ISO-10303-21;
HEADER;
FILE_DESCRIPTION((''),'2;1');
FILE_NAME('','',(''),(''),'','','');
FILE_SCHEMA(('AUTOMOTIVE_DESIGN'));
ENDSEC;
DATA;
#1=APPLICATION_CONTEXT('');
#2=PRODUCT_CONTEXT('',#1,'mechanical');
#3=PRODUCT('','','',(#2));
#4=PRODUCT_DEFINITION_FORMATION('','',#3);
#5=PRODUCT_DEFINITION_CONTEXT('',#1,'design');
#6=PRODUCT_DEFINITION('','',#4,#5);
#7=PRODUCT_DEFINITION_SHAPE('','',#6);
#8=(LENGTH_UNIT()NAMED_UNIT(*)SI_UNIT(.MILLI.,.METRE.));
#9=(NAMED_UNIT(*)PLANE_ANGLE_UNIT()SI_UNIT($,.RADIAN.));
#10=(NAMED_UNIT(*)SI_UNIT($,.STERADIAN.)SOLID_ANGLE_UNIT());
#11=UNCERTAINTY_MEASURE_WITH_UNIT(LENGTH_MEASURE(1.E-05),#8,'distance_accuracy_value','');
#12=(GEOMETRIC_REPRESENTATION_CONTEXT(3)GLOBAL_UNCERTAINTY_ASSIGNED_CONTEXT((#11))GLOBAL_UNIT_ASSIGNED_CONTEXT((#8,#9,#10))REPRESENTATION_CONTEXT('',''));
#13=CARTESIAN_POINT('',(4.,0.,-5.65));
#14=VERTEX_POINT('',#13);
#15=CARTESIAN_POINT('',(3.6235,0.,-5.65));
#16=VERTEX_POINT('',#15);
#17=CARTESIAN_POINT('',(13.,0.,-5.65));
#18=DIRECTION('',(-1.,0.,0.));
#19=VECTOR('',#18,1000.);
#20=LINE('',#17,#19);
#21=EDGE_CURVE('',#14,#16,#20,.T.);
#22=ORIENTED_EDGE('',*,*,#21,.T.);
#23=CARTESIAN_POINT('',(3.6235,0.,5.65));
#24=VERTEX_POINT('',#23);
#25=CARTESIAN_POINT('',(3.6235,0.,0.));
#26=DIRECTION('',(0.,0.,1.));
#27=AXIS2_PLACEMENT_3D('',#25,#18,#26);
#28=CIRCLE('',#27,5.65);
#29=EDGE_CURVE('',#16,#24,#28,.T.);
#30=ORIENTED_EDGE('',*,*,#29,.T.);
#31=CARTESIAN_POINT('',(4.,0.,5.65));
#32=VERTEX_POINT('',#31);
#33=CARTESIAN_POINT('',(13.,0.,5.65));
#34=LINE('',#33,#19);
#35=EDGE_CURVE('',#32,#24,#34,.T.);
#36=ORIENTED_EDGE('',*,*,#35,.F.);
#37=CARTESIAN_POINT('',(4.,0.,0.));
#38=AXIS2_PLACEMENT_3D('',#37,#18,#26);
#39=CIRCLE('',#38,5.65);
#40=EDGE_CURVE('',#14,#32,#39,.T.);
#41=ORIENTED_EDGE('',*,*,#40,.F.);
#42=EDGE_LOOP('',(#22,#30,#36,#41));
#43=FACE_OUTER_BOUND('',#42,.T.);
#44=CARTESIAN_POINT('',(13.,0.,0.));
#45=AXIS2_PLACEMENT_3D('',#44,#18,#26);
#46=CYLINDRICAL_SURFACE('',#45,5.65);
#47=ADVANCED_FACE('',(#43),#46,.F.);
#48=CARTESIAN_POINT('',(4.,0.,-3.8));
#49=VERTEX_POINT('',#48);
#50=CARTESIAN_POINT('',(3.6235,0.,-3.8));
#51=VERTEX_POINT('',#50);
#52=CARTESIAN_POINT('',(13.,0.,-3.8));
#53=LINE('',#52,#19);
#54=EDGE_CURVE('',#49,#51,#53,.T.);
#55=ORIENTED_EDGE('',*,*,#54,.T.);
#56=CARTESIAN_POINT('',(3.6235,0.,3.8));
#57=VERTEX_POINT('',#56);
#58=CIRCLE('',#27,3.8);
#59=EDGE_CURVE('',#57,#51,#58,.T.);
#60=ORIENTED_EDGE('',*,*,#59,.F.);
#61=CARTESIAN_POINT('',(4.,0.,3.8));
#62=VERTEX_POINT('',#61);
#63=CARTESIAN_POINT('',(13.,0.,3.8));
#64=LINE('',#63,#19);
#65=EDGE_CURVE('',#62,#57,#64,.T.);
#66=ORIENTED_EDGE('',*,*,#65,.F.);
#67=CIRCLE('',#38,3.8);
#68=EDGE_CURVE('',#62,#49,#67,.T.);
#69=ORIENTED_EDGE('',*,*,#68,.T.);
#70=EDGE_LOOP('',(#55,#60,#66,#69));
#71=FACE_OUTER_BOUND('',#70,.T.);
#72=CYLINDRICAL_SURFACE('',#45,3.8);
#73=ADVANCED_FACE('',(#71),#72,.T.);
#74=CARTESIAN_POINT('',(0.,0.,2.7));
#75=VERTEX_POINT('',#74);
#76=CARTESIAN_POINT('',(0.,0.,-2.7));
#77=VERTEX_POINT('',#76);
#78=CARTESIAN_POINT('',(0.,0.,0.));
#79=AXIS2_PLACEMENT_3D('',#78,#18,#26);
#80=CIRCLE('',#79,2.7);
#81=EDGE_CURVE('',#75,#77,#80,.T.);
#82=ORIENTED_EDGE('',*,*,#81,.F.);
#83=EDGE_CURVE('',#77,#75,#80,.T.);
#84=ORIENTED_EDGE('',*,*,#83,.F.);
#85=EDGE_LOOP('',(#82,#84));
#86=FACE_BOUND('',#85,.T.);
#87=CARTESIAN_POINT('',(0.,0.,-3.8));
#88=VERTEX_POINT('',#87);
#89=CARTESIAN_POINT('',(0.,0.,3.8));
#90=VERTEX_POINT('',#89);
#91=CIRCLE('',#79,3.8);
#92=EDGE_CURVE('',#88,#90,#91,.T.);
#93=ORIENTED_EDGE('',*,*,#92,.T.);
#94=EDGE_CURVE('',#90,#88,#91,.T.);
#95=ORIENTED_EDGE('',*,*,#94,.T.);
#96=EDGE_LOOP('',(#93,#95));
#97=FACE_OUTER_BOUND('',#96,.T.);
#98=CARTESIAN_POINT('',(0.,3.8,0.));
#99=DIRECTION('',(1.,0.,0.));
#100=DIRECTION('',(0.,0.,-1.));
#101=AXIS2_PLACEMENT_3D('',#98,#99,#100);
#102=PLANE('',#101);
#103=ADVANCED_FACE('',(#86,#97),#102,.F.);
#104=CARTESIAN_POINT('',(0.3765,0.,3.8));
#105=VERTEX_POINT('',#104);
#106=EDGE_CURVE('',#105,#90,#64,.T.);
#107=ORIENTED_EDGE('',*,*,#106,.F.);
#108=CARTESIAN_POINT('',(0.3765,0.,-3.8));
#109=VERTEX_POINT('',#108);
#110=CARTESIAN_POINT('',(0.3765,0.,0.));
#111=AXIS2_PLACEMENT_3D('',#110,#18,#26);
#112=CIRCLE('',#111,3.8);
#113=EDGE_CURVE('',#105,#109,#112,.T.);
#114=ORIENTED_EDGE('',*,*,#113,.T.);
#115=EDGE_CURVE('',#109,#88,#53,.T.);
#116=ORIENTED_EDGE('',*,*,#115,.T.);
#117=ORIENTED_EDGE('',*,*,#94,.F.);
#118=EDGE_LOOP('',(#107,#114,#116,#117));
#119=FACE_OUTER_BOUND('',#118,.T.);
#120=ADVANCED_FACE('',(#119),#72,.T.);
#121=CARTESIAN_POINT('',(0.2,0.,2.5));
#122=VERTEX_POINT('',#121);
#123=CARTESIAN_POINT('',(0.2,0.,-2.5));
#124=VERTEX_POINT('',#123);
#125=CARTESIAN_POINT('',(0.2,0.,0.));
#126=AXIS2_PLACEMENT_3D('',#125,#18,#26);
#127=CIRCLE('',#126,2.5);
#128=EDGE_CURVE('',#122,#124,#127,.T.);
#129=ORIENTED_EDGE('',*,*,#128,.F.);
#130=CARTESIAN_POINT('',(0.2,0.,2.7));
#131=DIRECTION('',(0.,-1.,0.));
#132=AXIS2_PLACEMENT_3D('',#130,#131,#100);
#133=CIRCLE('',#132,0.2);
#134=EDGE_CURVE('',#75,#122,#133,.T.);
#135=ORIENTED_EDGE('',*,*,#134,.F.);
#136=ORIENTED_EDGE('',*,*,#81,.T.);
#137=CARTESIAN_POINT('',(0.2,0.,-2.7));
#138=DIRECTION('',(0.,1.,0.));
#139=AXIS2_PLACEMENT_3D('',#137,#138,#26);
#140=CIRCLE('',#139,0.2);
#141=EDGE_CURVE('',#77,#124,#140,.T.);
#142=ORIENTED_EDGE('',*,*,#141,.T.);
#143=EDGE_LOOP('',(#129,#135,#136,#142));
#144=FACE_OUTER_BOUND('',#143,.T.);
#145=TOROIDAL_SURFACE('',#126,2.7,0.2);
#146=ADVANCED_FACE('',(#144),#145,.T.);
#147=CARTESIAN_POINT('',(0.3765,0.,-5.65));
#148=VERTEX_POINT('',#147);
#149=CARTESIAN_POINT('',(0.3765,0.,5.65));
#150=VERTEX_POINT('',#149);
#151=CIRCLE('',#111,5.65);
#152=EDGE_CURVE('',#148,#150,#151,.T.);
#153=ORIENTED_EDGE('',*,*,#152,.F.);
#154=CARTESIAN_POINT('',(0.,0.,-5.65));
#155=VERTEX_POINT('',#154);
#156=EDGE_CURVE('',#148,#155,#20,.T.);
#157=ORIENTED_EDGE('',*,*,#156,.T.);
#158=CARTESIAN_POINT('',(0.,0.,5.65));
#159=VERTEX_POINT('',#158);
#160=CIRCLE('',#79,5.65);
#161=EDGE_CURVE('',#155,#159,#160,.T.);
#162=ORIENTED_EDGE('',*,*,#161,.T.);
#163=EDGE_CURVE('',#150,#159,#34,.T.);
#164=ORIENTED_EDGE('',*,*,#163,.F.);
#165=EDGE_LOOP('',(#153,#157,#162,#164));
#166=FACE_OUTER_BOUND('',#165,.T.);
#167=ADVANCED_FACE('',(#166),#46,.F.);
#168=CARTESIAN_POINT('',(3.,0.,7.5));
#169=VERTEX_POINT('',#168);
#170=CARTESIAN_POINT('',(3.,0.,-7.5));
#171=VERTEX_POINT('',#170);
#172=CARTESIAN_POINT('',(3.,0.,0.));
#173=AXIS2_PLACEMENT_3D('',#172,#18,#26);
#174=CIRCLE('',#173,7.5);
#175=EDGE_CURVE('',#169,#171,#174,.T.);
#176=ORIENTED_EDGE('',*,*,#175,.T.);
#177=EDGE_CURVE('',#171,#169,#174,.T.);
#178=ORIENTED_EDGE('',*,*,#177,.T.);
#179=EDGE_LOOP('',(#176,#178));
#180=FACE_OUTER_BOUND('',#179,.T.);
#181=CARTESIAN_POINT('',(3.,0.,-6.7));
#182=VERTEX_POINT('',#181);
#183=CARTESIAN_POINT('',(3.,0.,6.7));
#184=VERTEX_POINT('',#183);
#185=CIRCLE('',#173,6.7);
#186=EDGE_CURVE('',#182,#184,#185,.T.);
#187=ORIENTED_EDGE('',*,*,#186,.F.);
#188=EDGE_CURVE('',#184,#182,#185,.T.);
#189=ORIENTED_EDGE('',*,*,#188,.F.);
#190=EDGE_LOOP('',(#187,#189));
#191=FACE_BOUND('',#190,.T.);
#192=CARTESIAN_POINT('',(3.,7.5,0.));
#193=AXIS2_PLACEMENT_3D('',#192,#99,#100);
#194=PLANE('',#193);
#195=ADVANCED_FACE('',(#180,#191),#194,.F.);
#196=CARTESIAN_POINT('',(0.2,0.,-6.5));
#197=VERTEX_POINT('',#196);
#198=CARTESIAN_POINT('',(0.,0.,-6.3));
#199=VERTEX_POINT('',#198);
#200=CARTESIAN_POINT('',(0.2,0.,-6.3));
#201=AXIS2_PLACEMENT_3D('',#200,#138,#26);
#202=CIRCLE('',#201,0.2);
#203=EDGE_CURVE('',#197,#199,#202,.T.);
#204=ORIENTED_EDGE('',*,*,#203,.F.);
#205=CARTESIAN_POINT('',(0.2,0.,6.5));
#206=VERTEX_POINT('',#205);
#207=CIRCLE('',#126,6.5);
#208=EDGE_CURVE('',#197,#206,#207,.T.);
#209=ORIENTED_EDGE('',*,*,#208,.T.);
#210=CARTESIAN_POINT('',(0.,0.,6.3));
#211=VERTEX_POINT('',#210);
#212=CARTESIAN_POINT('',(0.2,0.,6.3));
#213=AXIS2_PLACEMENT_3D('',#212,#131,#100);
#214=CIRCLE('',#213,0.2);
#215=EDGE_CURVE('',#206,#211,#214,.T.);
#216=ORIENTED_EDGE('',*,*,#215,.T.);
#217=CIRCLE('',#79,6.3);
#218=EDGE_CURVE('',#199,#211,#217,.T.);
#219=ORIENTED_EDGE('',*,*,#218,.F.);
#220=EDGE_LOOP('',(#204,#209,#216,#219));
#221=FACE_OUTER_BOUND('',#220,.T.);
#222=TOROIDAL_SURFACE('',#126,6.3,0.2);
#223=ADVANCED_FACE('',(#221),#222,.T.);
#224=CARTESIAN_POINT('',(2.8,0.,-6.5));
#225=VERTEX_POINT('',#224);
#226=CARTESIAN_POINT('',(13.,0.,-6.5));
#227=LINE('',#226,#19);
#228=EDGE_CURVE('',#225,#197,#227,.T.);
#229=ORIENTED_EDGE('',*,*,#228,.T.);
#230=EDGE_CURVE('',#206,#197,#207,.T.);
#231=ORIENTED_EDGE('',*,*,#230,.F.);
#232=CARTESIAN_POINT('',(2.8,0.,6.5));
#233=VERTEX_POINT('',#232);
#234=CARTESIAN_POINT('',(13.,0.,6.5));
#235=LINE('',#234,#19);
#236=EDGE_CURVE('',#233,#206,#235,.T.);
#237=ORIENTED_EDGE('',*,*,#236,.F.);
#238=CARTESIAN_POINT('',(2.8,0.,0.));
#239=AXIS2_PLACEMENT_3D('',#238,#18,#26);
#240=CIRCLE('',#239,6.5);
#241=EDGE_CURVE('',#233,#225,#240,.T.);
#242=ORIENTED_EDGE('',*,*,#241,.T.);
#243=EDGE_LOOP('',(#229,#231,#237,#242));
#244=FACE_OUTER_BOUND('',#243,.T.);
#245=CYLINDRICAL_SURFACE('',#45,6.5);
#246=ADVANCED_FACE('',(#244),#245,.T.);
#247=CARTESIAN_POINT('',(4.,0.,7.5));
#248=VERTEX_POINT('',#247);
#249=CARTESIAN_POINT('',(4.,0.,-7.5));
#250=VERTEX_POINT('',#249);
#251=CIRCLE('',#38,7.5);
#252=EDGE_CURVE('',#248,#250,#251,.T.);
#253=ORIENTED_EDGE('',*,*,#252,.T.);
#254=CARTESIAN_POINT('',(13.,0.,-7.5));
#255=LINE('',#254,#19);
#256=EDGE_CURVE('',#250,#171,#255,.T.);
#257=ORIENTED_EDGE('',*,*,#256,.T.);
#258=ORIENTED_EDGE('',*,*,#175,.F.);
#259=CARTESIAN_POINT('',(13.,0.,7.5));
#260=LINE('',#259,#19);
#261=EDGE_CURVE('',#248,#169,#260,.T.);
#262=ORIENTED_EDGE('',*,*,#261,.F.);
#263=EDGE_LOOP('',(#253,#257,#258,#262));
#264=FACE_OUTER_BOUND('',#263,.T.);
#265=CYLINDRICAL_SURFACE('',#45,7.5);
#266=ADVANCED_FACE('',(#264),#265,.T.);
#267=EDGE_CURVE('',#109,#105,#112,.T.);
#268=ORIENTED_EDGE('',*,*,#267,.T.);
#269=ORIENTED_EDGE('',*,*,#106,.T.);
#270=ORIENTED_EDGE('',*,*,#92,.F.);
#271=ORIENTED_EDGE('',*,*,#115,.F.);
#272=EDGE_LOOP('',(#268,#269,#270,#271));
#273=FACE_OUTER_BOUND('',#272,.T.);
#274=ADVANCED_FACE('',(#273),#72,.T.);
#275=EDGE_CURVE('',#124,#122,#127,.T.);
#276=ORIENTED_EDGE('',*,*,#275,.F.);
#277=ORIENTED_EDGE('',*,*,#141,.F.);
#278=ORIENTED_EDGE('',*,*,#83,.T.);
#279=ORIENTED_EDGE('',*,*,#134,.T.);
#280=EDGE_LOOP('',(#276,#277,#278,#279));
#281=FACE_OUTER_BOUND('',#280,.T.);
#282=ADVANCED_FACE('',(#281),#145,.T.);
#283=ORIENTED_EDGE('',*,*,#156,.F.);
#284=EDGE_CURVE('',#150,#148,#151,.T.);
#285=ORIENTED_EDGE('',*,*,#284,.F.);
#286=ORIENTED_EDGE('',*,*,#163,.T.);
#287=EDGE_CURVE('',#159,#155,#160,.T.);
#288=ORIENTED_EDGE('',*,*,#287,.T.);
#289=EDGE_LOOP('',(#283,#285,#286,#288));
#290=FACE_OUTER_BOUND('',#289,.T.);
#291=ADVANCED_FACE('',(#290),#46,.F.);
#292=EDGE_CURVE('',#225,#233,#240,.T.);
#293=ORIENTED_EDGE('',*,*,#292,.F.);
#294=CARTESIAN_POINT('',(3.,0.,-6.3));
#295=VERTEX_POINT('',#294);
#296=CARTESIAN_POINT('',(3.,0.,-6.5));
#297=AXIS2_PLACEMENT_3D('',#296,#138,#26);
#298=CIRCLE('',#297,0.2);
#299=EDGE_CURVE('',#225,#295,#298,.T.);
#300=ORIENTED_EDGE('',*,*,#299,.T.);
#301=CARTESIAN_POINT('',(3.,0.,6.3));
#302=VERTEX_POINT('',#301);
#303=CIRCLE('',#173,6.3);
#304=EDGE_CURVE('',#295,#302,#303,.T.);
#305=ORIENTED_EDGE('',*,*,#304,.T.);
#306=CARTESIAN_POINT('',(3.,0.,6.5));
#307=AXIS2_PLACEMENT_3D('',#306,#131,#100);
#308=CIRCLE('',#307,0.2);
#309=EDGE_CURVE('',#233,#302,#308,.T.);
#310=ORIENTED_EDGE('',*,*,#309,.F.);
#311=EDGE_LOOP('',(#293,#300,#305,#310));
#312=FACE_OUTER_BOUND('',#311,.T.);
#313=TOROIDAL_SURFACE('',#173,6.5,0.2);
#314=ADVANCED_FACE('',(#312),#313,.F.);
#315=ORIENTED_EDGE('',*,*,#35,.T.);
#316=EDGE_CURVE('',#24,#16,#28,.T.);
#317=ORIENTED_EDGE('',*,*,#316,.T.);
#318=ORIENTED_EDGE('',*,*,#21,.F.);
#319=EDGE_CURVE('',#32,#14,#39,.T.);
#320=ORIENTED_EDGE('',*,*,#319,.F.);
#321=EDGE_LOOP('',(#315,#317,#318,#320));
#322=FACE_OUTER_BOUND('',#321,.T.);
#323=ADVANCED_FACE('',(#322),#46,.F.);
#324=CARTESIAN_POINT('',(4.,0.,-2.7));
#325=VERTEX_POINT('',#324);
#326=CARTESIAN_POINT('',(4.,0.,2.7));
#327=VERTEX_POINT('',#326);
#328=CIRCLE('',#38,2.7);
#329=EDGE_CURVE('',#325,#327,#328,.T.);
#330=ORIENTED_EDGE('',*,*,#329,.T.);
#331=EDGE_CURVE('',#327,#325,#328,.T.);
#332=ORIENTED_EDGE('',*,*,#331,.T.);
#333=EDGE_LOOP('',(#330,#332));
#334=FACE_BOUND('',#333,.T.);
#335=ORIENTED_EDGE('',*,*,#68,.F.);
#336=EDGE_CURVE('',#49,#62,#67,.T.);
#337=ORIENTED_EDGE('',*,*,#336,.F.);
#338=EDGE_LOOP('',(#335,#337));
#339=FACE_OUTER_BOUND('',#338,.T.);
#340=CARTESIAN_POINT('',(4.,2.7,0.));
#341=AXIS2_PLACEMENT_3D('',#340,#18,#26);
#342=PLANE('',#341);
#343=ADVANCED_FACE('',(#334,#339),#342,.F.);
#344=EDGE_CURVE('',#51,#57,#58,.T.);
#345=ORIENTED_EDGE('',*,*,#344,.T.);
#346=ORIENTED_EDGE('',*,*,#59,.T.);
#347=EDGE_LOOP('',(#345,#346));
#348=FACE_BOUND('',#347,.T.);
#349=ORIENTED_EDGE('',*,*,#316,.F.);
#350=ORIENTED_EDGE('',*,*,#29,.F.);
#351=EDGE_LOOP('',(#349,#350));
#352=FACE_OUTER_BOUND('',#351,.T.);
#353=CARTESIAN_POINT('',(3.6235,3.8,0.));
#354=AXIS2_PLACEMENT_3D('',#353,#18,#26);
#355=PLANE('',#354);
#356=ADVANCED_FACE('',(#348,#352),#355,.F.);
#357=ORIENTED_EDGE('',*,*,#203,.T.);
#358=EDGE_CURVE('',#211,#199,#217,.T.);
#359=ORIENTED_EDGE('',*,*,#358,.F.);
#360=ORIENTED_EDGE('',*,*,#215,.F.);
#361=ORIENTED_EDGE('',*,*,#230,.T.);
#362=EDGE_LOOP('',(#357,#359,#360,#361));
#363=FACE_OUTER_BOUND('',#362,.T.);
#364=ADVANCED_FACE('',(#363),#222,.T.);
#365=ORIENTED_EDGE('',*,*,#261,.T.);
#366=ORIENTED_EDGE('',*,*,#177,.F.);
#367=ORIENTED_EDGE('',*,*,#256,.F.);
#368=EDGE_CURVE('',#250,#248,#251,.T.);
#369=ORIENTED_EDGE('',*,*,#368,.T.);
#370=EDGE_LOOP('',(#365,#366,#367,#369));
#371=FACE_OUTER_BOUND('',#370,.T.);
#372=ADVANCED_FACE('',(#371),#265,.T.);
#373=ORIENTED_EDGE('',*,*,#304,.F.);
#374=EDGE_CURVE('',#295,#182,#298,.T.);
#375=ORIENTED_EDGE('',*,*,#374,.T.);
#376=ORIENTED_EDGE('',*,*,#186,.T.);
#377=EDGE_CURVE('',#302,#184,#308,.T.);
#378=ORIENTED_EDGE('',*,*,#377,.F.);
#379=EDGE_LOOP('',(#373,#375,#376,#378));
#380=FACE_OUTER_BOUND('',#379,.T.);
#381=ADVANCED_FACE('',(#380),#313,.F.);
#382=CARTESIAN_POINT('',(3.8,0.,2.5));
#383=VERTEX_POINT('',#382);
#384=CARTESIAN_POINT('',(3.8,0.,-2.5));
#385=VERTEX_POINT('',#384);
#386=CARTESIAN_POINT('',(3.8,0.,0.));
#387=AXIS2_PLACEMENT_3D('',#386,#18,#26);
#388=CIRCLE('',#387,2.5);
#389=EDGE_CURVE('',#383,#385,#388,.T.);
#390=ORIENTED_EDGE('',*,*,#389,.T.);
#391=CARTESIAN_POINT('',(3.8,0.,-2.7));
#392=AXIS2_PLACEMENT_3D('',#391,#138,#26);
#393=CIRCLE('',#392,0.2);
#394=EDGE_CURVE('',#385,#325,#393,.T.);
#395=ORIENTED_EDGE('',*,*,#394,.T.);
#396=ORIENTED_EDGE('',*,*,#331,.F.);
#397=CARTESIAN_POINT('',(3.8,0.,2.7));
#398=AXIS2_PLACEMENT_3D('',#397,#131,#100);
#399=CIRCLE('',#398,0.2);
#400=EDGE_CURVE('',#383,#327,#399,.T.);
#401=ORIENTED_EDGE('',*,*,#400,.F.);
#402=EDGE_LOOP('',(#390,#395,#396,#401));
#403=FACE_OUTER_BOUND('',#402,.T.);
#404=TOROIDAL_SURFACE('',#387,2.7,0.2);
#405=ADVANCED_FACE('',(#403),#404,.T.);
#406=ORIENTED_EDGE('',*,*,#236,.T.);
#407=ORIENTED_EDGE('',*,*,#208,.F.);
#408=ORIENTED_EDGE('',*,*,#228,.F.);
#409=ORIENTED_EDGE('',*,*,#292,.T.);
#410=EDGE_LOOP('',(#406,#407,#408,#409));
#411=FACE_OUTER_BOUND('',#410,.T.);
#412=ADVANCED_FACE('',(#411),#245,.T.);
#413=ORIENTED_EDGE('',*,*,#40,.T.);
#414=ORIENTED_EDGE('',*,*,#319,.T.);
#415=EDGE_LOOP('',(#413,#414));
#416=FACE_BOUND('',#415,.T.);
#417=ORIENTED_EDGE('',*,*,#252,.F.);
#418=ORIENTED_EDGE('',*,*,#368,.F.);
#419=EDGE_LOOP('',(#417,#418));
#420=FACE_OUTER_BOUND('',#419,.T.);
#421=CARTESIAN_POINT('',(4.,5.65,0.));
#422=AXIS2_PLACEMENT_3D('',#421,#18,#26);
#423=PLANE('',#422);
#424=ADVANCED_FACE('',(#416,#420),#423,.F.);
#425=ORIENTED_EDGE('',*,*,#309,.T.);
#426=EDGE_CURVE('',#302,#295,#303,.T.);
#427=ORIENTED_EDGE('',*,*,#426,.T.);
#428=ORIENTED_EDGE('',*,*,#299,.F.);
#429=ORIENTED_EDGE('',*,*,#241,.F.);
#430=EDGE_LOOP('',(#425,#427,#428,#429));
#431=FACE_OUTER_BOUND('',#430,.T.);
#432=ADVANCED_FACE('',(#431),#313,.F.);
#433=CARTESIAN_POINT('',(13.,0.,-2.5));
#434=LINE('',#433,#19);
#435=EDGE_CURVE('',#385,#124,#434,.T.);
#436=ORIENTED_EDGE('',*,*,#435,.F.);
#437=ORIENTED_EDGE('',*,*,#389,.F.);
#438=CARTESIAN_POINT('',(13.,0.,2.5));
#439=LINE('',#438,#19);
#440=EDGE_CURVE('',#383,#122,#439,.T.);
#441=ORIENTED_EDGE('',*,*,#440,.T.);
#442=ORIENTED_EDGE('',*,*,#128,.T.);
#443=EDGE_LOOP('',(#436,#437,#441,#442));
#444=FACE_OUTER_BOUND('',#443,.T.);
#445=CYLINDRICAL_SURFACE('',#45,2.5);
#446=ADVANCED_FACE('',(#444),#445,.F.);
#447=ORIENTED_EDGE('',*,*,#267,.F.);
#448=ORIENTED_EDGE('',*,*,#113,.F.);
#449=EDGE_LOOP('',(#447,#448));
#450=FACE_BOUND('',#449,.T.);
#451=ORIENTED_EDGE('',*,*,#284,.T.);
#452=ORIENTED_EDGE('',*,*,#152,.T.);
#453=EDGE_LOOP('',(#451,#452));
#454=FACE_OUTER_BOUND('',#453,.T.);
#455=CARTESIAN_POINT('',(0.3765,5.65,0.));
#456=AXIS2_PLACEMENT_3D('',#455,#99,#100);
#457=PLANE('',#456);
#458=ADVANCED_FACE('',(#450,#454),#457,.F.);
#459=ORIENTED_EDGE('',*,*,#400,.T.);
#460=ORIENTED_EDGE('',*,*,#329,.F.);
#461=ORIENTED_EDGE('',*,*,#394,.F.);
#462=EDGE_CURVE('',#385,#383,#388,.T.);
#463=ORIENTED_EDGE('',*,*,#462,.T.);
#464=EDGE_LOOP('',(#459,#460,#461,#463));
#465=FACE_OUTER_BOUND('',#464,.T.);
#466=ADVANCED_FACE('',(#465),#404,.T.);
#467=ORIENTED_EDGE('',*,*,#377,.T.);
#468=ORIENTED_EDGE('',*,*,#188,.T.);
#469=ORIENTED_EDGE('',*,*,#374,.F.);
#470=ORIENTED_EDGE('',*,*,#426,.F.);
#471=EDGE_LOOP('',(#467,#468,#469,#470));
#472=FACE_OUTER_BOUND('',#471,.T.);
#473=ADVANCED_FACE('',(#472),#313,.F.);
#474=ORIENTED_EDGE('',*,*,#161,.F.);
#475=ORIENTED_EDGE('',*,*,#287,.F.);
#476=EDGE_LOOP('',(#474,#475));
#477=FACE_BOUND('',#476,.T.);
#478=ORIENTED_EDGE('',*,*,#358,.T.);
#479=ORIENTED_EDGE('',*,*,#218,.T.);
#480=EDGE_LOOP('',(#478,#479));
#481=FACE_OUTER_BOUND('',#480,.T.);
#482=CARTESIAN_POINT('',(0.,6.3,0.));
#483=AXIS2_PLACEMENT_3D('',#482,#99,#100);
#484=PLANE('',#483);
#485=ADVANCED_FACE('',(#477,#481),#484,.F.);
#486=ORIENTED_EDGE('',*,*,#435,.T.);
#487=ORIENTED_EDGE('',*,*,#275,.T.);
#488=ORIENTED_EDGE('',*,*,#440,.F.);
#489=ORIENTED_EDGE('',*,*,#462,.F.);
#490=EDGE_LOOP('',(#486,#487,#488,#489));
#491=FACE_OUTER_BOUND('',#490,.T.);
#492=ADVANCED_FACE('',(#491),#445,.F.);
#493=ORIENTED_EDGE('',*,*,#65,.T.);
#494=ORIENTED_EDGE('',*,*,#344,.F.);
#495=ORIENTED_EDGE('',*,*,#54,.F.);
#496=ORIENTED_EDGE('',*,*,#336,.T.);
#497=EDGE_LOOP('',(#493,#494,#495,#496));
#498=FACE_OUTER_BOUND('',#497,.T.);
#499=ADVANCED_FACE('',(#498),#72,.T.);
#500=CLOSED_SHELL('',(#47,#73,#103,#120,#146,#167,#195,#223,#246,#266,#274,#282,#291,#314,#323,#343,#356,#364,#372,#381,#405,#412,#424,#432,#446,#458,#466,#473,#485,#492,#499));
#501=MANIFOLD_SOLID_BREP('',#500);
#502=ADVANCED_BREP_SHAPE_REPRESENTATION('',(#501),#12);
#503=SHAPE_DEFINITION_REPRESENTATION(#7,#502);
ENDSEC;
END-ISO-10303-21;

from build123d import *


with BuildPart() as part:
    # Sketch1 → Revolve1 (revolve)
    with BuildSketch(Plane.XY, mode=Mode.PRIVATE) as revolve1_sk:
        with BuildLine():
            Line((0, 6.3), (0, 5.65))
            Line((0, 5.65), (0.3765, 5.65))
            Line((0.3765, 5.65), (0.3765, 3.8))
            Line((0.3765, 3.8), (0, 3.8))
            Line((0, 3.8), (0, 2.7))
            ThreePointArc((0, 2.7), (0.058578644, 2.558578644), (0.2, 2.5))
            Line((0.2, 2.5), (3.8, 2.5))
            ThreePointArc((3.8, 2.5), (3.941421356, 2.558578644), (4, 2.7))
            Line((4, 2.7), (4, 3.8))
            Line((4, 3.8), (3.6235, 3.8))
            Line((3.6235, 3.8), (3.6235, 5.65))
            Line((3.6235, 5.65), (4, 5.65))
            Line((4, 5.65), (4, 7.5))
            Line((4, 7.5), (3, 7.5))
            Line((3, 7.5), (3, 6.7))
            ThreePointArc((3, 6.7), (3.141421356, 6.358578644), (2.8, 6.5))
            Line((2.8, 6.5), (0.2, 6.5))
            ThreePointArc((0.2, 6.5), (0.058578644, 6.441421356), (0, 6.3))
        make_face()
    revolve(revolve1_sk.sketch.rotate(Axis((13, 0, 0), (-1, 0, 0)), 270), axis=Axis((13, 0, 0), (-1, 0, 0)))


solid = part.part
